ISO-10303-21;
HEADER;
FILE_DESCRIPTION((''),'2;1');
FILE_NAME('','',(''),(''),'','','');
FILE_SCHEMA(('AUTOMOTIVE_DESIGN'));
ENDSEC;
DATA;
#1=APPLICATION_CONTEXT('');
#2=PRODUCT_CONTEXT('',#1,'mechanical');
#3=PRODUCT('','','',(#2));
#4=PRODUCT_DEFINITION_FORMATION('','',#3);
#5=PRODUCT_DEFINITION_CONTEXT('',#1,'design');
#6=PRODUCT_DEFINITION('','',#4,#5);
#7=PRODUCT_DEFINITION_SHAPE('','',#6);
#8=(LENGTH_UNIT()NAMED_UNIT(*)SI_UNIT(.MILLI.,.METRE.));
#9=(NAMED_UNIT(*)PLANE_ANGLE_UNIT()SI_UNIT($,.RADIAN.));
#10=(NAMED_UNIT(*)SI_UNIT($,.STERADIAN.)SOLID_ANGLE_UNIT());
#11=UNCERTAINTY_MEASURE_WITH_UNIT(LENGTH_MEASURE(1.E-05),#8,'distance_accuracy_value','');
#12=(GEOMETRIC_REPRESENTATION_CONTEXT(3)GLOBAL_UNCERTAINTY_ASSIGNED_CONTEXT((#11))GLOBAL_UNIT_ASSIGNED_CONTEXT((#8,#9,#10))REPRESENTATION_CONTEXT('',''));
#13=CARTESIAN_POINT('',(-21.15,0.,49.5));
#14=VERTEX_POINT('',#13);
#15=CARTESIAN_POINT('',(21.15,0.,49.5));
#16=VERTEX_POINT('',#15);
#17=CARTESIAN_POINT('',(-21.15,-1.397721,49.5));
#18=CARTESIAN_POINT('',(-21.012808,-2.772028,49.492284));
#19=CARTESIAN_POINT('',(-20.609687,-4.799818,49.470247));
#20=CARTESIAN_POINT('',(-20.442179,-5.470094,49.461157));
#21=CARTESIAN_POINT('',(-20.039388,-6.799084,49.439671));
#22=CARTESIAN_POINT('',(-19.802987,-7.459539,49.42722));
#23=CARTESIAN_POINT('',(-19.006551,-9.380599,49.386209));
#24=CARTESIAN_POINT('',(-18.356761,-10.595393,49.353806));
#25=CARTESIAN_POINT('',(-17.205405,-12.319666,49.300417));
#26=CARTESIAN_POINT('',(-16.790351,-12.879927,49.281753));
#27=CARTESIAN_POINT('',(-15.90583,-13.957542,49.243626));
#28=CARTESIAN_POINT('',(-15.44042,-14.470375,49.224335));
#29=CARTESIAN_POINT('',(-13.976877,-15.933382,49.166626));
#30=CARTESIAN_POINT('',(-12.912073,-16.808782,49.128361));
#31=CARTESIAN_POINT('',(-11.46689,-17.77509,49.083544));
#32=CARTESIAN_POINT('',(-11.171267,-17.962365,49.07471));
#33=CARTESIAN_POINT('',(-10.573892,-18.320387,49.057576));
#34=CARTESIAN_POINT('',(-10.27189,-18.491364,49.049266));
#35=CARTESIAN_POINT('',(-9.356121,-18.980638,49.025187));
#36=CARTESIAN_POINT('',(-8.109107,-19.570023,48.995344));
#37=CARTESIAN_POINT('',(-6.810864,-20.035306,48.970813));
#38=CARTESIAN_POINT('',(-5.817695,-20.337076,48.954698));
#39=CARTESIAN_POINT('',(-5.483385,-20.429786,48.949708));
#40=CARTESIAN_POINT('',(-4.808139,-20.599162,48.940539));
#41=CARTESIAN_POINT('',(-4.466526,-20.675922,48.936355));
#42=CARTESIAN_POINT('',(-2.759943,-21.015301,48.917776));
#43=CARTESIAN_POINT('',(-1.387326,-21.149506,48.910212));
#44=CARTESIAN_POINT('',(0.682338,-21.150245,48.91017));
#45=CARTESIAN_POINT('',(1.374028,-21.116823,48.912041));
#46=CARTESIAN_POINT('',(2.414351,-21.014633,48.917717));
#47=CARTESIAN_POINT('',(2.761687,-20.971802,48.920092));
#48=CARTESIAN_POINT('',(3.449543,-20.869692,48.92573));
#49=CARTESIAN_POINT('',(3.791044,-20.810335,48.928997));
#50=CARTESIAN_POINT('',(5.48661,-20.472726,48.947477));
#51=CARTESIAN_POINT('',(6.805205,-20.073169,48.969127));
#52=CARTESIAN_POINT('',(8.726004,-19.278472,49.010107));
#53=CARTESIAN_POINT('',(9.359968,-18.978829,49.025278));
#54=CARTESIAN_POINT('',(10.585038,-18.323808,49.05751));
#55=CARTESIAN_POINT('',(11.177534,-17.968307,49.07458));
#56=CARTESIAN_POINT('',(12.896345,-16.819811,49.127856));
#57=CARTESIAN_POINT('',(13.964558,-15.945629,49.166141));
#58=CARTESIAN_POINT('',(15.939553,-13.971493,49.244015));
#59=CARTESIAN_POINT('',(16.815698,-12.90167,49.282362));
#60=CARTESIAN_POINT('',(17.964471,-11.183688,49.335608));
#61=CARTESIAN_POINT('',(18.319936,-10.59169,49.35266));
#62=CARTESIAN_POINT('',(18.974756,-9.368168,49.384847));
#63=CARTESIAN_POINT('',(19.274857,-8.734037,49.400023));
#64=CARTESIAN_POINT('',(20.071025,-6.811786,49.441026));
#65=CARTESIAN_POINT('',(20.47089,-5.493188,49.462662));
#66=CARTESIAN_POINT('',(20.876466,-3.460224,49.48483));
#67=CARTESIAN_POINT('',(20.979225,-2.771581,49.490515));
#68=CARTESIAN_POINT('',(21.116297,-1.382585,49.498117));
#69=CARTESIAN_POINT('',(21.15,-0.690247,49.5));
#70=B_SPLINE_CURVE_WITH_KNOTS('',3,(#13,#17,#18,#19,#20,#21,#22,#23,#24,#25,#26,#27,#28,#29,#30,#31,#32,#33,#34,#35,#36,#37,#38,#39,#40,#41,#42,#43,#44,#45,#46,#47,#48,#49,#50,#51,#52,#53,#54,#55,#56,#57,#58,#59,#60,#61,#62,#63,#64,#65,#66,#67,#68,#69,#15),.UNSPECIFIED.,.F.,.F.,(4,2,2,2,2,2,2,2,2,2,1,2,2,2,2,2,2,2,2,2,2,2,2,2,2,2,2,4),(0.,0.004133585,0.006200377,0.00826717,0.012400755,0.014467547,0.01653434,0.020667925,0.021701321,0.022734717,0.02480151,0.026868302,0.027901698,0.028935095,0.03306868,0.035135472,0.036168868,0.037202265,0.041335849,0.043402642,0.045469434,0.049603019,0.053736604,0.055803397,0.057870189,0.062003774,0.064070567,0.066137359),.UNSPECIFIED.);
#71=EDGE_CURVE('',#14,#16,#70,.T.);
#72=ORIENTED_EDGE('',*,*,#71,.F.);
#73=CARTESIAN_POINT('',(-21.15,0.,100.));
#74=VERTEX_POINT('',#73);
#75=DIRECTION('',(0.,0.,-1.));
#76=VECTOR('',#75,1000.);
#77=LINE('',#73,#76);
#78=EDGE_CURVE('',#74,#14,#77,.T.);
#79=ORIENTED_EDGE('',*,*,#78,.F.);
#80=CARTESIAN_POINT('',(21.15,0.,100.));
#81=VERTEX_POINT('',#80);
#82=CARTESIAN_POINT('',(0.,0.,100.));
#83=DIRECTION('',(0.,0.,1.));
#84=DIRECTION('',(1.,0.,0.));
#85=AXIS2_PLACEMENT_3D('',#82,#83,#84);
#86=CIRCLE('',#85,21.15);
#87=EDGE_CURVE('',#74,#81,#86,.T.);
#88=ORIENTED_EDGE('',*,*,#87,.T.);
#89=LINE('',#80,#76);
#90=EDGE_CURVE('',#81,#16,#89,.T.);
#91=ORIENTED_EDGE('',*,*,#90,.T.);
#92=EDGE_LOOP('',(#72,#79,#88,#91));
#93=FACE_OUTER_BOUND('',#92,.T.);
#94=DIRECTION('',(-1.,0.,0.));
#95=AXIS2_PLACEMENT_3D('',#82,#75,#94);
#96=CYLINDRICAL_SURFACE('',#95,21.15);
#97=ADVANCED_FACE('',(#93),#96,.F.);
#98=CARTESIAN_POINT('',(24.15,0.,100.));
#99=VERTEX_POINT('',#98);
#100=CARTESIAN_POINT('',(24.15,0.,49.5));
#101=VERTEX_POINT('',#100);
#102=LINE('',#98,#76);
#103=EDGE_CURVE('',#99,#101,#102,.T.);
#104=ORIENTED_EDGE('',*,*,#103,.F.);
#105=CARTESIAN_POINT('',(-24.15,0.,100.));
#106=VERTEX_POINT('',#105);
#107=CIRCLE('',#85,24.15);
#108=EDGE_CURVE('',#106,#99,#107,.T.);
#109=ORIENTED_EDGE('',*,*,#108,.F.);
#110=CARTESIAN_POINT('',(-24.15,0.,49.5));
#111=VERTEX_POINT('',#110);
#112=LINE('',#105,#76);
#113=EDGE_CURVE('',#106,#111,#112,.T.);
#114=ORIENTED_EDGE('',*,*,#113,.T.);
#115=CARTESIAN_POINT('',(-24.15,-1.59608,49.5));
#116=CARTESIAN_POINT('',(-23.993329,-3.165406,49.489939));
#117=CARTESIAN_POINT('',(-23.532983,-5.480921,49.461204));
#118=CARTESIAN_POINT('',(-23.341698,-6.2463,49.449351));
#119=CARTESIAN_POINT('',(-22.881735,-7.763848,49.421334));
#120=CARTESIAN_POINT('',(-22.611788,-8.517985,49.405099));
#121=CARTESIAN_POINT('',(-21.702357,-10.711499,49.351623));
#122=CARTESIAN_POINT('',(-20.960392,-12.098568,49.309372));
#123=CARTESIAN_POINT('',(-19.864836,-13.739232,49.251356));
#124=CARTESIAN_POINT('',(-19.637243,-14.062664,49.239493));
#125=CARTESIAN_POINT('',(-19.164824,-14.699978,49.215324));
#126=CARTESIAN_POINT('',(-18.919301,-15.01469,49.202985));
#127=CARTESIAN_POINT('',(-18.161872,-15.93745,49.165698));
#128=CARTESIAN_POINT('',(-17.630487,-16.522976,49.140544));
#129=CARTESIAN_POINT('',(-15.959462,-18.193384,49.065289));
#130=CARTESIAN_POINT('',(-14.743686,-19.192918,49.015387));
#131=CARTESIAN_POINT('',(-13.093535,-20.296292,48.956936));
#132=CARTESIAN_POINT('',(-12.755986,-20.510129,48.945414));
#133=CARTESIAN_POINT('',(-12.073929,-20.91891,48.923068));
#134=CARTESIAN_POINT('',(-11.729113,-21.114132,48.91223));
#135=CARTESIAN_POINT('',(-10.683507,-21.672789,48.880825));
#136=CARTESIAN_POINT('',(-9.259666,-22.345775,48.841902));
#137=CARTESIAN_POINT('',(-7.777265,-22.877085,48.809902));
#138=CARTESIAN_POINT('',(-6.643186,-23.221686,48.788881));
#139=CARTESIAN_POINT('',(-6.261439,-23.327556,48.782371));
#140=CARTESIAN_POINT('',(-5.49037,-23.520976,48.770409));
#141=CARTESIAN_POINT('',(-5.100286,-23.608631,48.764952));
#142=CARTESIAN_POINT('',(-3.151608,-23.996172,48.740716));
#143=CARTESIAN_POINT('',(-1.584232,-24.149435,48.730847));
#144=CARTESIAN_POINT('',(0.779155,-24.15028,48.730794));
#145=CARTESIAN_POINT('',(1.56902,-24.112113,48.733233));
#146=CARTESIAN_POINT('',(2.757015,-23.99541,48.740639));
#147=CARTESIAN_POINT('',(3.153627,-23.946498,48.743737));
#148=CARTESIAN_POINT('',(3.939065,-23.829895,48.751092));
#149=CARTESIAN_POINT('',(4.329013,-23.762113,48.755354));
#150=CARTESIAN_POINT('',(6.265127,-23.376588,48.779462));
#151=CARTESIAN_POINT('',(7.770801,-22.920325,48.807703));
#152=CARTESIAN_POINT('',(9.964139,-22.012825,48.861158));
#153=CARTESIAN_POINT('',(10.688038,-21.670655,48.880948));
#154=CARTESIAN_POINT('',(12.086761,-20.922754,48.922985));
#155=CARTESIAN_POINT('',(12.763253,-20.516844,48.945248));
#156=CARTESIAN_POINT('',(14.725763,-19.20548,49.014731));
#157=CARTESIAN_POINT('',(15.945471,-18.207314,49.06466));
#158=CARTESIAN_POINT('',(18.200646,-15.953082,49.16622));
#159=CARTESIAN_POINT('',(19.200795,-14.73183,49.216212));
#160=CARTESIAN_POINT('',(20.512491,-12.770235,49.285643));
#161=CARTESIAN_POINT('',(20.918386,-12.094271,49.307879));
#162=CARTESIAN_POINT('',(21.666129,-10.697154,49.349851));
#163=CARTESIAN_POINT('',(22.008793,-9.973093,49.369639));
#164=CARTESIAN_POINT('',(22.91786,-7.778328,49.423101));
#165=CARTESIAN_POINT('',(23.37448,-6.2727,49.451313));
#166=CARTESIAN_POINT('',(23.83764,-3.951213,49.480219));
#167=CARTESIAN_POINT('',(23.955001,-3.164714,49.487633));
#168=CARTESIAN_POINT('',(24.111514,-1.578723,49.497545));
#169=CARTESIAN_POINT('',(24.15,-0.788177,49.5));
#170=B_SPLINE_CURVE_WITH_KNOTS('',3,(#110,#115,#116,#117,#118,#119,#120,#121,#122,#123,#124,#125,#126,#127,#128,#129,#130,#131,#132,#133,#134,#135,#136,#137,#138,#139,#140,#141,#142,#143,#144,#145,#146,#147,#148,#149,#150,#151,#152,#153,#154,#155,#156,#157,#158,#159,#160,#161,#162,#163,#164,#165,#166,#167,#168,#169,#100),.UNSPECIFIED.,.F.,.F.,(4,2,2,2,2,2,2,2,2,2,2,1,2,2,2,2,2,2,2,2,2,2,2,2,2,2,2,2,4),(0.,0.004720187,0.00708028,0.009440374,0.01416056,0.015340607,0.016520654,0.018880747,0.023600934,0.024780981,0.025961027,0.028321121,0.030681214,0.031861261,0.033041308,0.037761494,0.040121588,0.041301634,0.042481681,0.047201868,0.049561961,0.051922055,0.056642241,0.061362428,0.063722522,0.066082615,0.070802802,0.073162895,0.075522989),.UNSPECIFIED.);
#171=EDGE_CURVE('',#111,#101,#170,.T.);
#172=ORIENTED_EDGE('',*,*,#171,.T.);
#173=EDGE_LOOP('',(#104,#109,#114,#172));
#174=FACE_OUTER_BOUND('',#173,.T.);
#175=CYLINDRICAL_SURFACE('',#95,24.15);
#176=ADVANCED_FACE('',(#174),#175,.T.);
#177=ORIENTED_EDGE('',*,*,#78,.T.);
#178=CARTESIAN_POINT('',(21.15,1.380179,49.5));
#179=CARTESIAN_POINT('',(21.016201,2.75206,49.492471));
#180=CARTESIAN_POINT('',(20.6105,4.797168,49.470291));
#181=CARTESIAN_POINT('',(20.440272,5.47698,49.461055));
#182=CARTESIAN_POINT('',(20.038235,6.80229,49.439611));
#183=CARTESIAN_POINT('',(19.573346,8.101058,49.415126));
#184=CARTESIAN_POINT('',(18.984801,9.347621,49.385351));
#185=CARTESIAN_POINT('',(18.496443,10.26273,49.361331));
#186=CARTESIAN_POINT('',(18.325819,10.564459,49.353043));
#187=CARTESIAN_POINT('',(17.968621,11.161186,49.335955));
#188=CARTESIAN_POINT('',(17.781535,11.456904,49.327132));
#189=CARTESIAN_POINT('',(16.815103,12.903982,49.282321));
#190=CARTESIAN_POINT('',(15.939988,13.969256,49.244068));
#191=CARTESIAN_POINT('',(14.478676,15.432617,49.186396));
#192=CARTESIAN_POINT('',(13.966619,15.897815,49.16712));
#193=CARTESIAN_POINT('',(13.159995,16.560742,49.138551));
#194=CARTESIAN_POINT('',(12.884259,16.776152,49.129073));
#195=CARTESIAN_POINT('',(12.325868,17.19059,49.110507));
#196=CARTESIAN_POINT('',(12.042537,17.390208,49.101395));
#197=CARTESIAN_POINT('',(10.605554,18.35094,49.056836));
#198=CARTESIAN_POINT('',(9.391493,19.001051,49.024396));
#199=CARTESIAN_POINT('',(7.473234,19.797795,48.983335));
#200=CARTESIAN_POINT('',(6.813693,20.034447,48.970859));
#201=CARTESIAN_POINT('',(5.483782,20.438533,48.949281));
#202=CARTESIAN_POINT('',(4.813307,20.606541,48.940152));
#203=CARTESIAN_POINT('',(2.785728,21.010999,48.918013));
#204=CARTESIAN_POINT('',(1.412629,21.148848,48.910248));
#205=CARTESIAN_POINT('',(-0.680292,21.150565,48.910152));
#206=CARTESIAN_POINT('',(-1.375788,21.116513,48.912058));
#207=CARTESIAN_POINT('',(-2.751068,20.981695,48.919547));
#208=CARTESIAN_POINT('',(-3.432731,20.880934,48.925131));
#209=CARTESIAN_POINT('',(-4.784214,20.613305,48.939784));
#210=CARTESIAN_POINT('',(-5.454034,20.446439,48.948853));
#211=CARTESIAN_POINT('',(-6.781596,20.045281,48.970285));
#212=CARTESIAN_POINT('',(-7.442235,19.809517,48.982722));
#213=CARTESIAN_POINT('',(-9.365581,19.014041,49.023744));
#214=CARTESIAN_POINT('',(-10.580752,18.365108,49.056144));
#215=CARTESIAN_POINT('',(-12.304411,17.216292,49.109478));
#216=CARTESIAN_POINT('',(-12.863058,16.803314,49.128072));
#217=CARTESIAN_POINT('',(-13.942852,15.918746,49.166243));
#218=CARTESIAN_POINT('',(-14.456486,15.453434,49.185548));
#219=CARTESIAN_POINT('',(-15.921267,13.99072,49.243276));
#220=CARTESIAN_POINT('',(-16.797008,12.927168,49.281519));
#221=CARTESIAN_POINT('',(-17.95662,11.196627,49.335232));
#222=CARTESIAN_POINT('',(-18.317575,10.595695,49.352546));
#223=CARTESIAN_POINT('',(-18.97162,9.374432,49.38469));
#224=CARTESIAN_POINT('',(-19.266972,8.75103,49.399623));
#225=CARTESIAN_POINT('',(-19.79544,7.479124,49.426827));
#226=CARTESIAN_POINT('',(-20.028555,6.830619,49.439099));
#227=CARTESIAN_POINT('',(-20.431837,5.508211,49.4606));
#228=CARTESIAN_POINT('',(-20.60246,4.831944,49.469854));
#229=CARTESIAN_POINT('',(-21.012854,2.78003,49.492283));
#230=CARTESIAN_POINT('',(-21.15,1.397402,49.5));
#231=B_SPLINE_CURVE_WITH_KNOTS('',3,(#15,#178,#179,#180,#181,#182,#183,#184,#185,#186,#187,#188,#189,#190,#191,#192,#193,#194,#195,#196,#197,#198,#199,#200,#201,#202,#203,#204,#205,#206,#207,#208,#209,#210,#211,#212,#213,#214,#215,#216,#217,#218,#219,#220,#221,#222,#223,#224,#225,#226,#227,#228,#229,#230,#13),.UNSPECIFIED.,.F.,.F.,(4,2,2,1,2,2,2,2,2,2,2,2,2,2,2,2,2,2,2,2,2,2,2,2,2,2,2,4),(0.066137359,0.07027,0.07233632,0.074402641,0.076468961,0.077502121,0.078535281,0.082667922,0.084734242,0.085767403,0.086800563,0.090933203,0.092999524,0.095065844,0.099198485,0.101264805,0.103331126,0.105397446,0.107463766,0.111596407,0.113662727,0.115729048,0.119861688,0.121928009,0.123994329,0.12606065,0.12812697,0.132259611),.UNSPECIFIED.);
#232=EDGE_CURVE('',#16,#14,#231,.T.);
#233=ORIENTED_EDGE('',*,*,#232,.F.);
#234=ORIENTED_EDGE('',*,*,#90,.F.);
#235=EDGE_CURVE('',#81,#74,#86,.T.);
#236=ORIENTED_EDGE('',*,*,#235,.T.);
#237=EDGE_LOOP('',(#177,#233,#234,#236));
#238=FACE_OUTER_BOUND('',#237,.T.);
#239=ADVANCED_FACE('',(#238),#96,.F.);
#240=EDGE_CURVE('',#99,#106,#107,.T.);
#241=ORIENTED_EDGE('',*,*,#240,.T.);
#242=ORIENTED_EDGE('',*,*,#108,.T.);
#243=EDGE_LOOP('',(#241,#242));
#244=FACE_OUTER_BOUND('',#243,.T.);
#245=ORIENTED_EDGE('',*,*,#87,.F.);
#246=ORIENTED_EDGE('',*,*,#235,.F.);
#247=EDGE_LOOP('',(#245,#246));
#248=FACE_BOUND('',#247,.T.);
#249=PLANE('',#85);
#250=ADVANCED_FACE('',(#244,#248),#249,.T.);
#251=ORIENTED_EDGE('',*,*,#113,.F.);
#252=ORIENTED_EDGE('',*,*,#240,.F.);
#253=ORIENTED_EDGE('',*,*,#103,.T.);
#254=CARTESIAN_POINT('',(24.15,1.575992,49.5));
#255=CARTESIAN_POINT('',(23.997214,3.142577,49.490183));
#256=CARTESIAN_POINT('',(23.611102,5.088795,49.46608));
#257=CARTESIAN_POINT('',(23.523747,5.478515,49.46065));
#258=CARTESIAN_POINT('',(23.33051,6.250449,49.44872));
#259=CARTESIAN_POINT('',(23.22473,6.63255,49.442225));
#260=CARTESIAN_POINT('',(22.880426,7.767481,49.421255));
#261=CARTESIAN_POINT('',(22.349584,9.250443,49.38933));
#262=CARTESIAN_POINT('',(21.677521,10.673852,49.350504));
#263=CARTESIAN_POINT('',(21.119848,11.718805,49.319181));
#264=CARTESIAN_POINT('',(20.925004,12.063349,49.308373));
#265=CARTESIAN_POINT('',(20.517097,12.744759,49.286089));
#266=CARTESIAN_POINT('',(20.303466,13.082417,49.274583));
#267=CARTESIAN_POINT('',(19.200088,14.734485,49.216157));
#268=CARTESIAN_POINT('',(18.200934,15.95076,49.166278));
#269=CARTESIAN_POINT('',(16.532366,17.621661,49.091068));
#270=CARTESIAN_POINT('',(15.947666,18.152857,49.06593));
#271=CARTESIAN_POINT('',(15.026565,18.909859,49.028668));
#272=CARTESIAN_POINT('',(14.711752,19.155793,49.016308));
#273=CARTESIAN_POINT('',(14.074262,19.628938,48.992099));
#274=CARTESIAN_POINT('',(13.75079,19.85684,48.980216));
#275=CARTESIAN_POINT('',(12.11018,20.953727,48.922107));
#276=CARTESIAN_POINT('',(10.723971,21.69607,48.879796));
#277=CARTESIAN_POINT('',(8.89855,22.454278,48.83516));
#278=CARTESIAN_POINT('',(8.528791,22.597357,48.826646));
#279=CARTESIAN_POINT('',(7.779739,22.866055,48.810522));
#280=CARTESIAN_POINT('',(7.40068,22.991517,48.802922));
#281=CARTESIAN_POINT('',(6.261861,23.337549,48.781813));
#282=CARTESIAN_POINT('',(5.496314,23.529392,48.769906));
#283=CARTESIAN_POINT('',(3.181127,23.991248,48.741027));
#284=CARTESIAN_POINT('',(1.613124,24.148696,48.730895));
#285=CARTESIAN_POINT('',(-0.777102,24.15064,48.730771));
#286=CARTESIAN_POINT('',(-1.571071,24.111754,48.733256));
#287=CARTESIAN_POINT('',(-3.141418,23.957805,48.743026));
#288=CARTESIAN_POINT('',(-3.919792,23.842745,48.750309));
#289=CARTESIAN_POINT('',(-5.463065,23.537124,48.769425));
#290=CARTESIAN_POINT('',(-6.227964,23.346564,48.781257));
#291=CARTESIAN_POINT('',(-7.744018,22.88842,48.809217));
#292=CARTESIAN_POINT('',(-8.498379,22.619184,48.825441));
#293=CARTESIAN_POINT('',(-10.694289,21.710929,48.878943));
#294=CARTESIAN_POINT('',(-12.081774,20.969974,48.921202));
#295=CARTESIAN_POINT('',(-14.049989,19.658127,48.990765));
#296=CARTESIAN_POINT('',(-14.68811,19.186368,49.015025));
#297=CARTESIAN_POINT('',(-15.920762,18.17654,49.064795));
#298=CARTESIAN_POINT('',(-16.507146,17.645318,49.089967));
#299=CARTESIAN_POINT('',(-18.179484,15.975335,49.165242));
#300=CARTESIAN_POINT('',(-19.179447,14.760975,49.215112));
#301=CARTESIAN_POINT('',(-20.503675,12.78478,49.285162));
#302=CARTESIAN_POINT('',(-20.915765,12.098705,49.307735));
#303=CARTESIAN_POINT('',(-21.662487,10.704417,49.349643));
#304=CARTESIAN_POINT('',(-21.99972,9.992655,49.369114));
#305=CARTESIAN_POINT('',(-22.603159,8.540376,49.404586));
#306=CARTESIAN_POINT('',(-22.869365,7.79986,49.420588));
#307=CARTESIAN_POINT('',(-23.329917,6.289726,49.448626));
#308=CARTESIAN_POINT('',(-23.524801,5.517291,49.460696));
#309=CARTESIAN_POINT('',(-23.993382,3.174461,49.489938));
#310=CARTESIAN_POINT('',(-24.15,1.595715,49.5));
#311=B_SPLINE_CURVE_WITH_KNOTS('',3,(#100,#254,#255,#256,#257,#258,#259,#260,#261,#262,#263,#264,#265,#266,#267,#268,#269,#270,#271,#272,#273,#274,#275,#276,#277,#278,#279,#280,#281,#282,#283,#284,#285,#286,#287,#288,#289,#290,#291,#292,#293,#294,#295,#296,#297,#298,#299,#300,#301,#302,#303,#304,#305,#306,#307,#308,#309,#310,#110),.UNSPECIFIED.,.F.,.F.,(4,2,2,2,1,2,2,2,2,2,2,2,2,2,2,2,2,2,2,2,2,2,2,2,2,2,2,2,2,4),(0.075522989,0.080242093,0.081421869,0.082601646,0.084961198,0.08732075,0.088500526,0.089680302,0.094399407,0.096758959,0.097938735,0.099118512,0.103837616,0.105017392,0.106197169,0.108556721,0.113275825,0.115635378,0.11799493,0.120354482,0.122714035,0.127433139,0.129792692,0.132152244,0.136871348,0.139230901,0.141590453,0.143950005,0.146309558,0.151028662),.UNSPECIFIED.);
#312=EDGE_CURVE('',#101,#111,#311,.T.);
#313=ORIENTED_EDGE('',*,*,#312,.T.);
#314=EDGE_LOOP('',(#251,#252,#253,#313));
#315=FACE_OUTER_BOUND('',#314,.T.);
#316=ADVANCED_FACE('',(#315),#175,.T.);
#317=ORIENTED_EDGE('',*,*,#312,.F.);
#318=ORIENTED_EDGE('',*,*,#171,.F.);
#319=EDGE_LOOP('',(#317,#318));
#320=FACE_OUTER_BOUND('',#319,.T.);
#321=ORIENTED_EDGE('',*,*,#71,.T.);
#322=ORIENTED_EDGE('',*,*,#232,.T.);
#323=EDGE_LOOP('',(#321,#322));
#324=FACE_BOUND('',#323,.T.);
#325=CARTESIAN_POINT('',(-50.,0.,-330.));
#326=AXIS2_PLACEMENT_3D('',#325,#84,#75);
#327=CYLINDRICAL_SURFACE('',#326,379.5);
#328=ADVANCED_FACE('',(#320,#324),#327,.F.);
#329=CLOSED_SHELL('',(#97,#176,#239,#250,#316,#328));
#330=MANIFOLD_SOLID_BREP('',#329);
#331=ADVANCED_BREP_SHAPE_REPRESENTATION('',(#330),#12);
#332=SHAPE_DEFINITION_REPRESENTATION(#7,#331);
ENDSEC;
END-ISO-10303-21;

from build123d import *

# Parameters (mm, degrees)
SKETCH1_R           = 24.15
SKETCH1_R_2         = 21.15
BOSS_EXTRUDE1_DEPTH = 100
SKETCH3_R           = 379.5
CUT_EXTRUDE2_DEPTH  = 50


with BuildPart() as part:
    # Sketch1 → Boss-Extrude1 (new body)
    with BuildSketch(Plane.XY):
        Circle(SKETCH1_R)
        Circle(SKETCH1_R_2, mode=Mode.SUBTRACT)
    extrude(amount=BOSS_EXTRUDE1_DEPTH)

    # Sketch3 → Cut-Extrude2 (cut, symmetric)
    with BuildSketch(Plane(origin=(0, 0, 0), x_dir=(0, 0, -1), z_dir=(1, 0, 0))):
        with Locations((330, 0)):
            Circle(SKETCH3_R)
    extrude(amount=CUT_EXTRUDE2_DEPTH, both=True, mode=Mode.SUBTRACT)


solid = part.part
